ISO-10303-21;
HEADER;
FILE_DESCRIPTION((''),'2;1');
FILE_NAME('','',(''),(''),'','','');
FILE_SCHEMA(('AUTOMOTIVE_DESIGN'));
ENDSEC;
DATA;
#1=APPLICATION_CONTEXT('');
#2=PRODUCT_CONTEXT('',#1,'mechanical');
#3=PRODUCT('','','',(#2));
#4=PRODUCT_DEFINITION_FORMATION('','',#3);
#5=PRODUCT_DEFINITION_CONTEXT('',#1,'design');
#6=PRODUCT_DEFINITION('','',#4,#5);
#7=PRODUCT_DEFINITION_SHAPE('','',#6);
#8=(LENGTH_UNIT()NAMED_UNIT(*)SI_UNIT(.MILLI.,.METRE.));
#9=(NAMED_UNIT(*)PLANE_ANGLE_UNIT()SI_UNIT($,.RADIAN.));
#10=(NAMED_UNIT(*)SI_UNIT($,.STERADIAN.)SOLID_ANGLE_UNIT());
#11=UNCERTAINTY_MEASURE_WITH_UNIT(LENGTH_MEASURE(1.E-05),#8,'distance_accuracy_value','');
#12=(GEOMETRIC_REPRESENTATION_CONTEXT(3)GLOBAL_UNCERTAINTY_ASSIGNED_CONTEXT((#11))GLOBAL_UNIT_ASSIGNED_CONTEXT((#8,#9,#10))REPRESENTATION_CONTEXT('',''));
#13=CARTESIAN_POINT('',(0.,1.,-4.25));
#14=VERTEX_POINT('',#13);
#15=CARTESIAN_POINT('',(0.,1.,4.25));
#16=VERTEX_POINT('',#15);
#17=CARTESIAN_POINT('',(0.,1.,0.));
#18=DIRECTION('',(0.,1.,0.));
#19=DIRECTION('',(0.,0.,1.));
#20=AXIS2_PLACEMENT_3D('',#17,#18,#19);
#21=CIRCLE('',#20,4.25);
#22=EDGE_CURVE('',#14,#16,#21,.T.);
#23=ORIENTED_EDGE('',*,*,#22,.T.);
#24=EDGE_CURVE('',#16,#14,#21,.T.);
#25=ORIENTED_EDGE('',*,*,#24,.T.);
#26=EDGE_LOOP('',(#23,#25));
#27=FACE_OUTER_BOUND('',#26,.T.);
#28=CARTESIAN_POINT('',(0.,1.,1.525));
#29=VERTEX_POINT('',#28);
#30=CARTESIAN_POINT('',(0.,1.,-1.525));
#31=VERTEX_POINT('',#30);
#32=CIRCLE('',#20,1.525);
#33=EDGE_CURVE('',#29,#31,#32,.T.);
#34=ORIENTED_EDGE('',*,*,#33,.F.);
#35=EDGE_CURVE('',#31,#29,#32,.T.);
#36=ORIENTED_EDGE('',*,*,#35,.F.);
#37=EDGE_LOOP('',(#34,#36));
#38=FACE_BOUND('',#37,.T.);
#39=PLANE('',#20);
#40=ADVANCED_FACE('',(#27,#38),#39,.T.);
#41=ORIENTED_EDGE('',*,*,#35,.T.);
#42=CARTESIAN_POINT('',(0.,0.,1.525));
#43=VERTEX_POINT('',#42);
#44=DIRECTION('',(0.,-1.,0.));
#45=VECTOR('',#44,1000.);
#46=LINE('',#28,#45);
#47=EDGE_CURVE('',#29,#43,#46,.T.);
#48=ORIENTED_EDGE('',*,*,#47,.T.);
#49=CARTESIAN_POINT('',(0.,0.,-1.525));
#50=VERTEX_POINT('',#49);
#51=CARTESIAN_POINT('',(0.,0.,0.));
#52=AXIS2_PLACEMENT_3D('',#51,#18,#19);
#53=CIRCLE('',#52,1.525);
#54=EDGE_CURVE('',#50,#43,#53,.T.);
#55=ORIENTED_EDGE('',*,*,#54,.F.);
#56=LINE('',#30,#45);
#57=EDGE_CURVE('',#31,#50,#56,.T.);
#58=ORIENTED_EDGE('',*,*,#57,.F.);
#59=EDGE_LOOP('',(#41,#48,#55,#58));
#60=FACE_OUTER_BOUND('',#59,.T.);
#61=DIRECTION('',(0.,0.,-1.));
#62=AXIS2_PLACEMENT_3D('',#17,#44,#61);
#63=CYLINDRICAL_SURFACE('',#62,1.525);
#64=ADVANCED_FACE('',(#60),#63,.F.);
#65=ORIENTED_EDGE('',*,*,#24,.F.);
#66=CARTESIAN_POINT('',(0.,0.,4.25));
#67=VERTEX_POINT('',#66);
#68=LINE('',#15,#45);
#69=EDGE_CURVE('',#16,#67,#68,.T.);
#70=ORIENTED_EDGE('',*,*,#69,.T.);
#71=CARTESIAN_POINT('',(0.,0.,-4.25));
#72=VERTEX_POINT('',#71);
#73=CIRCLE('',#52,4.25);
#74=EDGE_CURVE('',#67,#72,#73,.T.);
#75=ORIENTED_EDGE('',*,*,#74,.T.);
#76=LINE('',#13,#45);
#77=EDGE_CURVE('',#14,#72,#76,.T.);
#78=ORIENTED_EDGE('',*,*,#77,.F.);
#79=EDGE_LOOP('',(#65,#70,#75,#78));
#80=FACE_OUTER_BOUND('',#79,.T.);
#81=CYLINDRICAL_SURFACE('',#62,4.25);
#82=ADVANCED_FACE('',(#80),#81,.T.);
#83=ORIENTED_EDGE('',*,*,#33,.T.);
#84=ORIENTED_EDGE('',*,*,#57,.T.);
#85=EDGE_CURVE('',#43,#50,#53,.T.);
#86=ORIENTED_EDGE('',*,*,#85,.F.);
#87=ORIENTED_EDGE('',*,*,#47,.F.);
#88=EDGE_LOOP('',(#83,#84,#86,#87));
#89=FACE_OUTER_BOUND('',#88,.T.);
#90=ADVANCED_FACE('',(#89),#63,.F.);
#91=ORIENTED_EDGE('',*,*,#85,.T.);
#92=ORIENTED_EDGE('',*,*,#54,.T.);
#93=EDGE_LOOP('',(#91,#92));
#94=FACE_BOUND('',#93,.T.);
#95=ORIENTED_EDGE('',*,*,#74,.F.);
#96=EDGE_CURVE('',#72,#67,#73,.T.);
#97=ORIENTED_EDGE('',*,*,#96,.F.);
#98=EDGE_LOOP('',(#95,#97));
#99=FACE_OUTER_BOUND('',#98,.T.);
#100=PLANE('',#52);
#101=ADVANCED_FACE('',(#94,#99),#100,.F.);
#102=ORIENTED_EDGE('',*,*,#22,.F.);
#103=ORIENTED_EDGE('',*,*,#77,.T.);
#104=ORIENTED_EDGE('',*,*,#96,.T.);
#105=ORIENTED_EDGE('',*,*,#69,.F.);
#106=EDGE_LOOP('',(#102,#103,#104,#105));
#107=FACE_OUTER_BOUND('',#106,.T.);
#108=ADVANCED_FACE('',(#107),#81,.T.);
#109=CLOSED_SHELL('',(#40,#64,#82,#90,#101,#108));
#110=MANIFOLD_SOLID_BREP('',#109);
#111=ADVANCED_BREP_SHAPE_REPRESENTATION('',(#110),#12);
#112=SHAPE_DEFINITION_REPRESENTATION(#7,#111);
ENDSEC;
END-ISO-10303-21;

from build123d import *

# Parameters (mm, degrees)
SKETCH1_R           = 4.25
SKETCH1_R_2         = 1.525
BOSS_EXTRUDE1_DEPTH = 1


with BuildPart() as part:
    # Sketch1 → Boss-Extrude1 (new body)
    with BuildSketch(Plane(origin=(0, 0, 0), x_dir=(1, 0, 0), z_dir=(0, 1, 0))):
        with Locations(Location((0, 0, 0), (0, 0, 270))):
            Circle(SKETCH1_R)
        with Locations(Location((0, 0, 0), (0, 0, 270))):
            Circle(SKETCH1_R_2, mode=Mode.SUBTRACT)
    extrude(amount=BOSS_EXTRUDE1_DEPTH)


solid = part.part
